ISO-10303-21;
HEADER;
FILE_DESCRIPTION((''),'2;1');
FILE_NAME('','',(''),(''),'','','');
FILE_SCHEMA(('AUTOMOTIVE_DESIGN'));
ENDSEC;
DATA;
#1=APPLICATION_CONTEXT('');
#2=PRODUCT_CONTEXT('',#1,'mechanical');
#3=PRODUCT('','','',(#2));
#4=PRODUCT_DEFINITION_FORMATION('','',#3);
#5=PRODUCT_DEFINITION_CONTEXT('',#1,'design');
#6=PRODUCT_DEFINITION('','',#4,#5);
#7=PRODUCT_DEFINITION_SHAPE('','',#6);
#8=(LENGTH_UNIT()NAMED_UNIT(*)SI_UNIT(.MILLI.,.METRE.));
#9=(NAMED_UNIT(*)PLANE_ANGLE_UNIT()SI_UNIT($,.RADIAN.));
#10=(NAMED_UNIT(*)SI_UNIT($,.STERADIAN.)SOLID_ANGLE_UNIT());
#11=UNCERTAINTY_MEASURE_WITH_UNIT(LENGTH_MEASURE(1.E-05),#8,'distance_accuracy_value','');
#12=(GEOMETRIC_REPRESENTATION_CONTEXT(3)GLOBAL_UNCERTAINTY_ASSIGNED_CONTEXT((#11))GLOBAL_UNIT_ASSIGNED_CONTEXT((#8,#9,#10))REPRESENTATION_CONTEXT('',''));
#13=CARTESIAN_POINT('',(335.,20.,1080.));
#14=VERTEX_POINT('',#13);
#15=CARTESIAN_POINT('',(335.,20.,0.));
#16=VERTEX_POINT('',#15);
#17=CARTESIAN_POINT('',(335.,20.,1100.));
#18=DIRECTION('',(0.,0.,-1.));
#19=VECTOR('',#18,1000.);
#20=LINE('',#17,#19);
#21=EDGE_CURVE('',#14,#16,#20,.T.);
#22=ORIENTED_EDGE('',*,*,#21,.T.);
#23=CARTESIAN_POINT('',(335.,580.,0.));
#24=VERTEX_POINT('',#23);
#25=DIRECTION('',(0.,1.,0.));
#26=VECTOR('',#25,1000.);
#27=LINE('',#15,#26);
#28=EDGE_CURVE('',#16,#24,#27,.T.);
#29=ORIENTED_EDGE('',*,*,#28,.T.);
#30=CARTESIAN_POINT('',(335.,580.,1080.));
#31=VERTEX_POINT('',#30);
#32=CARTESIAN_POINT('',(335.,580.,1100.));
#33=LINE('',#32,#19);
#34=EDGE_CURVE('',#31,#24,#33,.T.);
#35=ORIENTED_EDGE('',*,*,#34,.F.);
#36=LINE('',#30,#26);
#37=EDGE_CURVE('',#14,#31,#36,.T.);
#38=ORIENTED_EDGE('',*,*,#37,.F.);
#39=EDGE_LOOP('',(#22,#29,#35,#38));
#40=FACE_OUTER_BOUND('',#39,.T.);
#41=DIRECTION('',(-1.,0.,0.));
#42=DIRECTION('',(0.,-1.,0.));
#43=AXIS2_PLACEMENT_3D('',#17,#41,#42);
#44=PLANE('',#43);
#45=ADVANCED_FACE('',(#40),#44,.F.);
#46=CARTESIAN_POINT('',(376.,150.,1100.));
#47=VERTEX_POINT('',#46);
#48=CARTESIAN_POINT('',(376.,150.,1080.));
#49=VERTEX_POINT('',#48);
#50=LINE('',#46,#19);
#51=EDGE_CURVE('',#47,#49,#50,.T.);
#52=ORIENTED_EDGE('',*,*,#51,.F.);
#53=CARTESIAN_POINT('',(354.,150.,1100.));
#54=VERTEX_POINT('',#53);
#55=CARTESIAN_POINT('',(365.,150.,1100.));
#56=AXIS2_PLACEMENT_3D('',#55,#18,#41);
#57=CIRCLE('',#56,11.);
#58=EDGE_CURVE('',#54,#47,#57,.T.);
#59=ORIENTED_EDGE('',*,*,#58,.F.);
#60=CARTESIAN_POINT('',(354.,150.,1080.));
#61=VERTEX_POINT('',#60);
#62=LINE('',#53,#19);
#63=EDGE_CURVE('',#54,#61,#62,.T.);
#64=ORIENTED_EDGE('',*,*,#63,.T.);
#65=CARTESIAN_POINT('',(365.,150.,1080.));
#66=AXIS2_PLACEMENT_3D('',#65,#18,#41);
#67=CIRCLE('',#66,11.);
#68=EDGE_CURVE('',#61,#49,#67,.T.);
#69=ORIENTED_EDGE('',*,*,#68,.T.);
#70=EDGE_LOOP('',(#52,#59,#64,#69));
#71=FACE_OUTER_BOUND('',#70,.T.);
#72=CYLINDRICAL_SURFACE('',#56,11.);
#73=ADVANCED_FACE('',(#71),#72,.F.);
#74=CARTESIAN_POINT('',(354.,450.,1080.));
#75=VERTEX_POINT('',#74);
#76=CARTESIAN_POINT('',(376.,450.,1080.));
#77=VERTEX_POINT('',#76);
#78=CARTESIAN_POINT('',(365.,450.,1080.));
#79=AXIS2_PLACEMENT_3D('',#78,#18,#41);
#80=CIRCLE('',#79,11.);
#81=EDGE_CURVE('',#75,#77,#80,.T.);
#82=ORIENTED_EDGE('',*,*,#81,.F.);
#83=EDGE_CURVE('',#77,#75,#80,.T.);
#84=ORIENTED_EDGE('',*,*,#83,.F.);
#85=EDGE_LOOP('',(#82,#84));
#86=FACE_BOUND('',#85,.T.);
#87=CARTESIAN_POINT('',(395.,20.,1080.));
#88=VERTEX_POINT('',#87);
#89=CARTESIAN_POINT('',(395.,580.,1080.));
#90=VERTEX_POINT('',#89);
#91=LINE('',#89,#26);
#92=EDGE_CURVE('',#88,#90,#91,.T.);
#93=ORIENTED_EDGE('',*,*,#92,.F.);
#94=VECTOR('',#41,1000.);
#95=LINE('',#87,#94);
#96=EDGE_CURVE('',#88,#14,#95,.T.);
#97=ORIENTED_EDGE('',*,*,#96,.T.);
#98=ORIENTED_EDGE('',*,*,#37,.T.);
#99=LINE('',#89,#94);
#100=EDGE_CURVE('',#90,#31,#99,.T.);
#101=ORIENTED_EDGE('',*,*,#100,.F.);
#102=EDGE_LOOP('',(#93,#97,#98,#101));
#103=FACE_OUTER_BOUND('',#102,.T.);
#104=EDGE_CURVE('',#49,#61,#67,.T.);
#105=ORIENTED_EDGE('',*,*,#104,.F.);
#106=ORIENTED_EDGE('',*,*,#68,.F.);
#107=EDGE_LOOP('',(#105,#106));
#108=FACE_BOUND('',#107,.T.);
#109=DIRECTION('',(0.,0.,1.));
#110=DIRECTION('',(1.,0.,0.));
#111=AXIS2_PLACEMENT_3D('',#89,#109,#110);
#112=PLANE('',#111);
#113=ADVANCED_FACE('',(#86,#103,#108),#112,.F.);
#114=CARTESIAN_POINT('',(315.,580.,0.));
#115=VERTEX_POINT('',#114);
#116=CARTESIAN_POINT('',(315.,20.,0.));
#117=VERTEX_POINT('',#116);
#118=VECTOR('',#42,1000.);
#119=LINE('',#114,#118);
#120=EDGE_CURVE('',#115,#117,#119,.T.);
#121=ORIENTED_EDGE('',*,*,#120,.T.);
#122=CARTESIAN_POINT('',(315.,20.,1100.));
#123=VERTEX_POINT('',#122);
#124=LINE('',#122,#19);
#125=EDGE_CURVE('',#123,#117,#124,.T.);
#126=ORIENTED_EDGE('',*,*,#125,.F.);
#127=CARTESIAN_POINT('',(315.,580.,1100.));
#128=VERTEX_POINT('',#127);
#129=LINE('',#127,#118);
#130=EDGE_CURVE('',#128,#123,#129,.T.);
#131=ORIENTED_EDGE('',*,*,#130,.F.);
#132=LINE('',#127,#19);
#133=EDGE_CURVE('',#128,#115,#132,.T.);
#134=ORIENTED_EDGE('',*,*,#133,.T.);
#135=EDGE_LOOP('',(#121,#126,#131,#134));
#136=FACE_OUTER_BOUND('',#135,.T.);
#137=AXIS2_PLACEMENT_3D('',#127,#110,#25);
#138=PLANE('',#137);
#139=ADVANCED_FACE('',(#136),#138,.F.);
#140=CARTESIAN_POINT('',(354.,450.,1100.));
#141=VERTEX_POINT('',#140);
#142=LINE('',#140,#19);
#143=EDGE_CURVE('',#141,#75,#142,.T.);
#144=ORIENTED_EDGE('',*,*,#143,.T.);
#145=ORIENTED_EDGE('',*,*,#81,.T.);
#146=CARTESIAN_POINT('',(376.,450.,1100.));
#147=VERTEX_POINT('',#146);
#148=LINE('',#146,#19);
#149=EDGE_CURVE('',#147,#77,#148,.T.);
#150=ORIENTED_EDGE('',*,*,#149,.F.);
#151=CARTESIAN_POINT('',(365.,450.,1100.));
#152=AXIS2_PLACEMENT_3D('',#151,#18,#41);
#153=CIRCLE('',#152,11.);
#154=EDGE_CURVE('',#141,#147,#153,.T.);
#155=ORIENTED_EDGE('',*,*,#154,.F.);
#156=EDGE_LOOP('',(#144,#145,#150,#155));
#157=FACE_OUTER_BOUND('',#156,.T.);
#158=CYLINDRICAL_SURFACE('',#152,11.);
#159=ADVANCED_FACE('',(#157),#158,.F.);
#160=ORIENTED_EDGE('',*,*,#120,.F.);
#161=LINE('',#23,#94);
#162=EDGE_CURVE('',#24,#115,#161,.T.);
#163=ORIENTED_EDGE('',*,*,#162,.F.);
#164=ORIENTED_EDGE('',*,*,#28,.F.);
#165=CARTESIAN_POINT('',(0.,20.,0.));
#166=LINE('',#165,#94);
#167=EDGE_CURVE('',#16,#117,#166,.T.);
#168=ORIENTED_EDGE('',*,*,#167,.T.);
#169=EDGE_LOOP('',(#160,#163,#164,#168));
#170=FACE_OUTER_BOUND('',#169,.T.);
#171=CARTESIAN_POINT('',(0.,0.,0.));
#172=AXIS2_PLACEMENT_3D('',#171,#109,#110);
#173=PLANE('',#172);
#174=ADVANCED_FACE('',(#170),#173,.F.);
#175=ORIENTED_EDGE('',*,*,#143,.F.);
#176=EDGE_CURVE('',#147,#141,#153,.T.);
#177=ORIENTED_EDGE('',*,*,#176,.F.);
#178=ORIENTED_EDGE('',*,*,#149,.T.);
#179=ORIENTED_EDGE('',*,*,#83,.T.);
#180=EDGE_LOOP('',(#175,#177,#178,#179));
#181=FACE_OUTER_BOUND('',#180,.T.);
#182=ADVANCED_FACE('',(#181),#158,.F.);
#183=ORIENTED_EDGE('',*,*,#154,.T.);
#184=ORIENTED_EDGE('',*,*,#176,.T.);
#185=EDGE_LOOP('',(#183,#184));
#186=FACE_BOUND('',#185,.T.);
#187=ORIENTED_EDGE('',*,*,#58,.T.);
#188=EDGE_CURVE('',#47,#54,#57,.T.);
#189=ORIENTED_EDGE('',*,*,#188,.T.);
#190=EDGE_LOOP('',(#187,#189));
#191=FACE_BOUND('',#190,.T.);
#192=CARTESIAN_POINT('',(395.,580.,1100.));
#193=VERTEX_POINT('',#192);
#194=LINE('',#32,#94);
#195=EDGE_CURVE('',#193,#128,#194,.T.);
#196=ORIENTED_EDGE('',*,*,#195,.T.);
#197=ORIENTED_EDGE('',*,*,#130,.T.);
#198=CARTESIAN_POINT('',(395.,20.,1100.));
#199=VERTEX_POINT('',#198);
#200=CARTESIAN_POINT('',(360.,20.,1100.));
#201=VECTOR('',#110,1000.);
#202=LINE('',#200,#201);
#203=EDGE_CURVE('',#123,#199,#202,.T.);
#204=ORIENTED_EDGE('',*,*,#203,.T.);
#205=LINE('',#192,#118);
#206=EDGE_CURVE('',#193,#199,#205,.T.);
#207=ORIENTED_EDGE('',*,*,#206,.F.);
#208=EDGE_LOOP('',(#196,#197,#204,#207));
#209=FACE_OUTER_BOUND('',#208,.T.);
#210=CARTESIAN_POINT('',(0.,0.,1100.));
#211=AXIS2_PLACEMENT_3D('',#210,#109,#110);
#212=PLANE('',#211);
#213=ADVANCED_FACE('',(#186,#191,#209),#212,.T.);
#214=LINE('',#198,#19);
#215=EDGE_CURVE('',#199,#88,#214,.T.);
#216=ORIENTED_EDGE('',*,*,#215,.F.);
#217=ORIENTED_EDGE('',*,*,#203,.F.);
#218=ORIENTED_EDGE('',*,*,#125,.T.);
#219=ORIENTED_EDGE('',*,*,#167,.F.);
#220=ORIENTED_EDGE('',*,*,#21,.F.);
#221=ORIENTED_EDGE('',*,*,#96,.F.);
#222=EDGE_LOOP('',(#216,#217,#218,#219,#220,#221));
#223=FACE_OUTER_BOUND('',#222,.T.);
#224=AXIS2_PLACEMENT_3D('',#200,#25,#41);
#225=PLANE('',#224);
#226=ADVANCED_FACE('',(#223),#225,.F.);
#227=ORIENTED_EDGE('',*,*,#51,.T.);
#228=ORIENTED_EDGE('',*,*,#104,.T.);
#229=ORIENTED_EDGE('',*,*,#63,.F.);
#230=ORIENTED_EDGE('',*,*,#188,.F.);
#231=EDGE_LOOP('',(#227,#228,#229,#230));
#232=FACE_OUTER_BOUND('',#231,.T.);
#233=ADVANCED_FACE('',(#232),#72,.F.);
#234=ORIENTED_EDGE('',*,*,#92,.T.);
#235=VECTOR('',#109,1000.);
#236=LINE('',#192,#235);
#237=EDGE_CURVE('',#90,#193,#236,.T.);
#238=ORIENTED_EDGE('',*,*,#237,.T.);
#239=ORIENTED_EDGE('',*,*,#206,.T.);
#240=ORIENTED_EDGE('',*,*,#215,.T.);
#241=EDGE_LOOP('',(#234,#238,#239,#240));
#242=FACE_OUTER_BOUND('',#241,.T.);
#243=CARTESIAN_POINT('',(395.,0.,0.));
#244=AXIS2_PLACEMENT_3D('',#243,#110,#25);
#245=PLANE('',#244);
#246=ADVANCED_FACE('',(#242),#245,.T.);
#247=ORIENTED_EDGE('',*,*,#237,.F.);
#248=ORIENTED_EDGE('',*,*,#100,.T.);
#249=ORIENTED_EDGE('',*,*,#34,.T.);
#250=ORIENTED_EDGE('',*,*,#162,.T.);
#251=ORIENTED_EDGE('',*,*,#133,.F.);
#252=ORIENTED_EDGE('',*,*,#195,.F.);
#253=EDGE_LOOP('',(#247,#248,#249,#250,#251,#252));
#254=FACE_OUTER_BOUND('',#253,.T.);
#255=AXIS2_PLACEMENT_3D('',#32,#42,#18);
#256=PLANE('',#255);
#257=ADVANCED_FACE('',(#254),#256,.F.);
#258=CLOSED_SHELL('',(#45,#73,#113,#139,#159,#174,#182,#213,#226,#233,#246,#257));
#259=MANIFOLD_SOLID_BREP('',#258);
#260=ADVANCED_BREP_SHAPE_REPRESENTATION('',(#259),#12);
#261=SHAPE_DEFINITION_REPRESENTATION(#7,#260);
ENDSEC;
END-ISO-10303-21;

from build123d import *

# Parameters (mm, degrees)
BOSS_EXTRUDE1_DEPTH = 1100
CUT_EXTRUDE1_DEPTH  = 1295.604186615
SKETCH3_W           = 20
SKETCH3_H           = 560
BOSS_EXTRUDE2_DEPTH = 60
SKETCH4_R           = 11
CUT_EXTRUDE2_DEPTH  = 1288.953803519


with BuildPart() as part:
    # Sketch1 → Boss-Extrude1 (new body)
    with BuildSketch(Plane.XY):
        Polygon((360, 0), (-360, 0), (-360, 20), (-335, 20), (-335, 580), (-315, 580), (-315, 20), (315, 20), (315, 580), (335, 580), (335, 20), (360, 20), align=None)
    extrude(amount=BOSS_EXTRUDE1_DEPTH)

    # Sketch2 → Cut-Extrude1 (cut, through all)
    with BuildSketch(Plane(origin=(0, 0, 0), x_dir=(-1, 0, 0), z_dir=(0, 0, -1))):
        Polygon((-360, 20), (-59.240800915, 20), (-59.240800915, 755.063041929), (647.427412598, 706.251760561), (560.651801276, -150.657401245), (-360, -188.621731198), (-684.035873625, -70.661134557), align=None)
    extrude(amount=-CUT_EXTRUDE1_DEPTH, mode=Mode.SUBTRACT)

    # Sketch3 → Boss-Extrude2 (add)
    with BuildSketch(Plane(origin=(335, 0, 0), x_dir=(0, 0, -1), z_dir=(1, 0, 0))):
        with Locations((-1090, 300)):
            Rectangle(SKETCH3_W, SKETCH3_H)
    extrude(amount=BOSS_EXTRUDE2_DEPTH)

    # Sketch4 → Cut-Extrude2 (cut, through all)
    with BuildSketch(Plane(origin=(0, 0, 1080), x_dir=(-1, 0, 0), z_dir=(0, 0, -1))):
        with Locations((-365, 450)):
            Circle(SKETCH4_R)
        with Locations((-365, 150)):
            Circle(SKETCH4_R)
    extrude(amount=-CUT_EXTRUDE2_DEPTH, mode=Mode.SUBTRACT)


solid = part.part
